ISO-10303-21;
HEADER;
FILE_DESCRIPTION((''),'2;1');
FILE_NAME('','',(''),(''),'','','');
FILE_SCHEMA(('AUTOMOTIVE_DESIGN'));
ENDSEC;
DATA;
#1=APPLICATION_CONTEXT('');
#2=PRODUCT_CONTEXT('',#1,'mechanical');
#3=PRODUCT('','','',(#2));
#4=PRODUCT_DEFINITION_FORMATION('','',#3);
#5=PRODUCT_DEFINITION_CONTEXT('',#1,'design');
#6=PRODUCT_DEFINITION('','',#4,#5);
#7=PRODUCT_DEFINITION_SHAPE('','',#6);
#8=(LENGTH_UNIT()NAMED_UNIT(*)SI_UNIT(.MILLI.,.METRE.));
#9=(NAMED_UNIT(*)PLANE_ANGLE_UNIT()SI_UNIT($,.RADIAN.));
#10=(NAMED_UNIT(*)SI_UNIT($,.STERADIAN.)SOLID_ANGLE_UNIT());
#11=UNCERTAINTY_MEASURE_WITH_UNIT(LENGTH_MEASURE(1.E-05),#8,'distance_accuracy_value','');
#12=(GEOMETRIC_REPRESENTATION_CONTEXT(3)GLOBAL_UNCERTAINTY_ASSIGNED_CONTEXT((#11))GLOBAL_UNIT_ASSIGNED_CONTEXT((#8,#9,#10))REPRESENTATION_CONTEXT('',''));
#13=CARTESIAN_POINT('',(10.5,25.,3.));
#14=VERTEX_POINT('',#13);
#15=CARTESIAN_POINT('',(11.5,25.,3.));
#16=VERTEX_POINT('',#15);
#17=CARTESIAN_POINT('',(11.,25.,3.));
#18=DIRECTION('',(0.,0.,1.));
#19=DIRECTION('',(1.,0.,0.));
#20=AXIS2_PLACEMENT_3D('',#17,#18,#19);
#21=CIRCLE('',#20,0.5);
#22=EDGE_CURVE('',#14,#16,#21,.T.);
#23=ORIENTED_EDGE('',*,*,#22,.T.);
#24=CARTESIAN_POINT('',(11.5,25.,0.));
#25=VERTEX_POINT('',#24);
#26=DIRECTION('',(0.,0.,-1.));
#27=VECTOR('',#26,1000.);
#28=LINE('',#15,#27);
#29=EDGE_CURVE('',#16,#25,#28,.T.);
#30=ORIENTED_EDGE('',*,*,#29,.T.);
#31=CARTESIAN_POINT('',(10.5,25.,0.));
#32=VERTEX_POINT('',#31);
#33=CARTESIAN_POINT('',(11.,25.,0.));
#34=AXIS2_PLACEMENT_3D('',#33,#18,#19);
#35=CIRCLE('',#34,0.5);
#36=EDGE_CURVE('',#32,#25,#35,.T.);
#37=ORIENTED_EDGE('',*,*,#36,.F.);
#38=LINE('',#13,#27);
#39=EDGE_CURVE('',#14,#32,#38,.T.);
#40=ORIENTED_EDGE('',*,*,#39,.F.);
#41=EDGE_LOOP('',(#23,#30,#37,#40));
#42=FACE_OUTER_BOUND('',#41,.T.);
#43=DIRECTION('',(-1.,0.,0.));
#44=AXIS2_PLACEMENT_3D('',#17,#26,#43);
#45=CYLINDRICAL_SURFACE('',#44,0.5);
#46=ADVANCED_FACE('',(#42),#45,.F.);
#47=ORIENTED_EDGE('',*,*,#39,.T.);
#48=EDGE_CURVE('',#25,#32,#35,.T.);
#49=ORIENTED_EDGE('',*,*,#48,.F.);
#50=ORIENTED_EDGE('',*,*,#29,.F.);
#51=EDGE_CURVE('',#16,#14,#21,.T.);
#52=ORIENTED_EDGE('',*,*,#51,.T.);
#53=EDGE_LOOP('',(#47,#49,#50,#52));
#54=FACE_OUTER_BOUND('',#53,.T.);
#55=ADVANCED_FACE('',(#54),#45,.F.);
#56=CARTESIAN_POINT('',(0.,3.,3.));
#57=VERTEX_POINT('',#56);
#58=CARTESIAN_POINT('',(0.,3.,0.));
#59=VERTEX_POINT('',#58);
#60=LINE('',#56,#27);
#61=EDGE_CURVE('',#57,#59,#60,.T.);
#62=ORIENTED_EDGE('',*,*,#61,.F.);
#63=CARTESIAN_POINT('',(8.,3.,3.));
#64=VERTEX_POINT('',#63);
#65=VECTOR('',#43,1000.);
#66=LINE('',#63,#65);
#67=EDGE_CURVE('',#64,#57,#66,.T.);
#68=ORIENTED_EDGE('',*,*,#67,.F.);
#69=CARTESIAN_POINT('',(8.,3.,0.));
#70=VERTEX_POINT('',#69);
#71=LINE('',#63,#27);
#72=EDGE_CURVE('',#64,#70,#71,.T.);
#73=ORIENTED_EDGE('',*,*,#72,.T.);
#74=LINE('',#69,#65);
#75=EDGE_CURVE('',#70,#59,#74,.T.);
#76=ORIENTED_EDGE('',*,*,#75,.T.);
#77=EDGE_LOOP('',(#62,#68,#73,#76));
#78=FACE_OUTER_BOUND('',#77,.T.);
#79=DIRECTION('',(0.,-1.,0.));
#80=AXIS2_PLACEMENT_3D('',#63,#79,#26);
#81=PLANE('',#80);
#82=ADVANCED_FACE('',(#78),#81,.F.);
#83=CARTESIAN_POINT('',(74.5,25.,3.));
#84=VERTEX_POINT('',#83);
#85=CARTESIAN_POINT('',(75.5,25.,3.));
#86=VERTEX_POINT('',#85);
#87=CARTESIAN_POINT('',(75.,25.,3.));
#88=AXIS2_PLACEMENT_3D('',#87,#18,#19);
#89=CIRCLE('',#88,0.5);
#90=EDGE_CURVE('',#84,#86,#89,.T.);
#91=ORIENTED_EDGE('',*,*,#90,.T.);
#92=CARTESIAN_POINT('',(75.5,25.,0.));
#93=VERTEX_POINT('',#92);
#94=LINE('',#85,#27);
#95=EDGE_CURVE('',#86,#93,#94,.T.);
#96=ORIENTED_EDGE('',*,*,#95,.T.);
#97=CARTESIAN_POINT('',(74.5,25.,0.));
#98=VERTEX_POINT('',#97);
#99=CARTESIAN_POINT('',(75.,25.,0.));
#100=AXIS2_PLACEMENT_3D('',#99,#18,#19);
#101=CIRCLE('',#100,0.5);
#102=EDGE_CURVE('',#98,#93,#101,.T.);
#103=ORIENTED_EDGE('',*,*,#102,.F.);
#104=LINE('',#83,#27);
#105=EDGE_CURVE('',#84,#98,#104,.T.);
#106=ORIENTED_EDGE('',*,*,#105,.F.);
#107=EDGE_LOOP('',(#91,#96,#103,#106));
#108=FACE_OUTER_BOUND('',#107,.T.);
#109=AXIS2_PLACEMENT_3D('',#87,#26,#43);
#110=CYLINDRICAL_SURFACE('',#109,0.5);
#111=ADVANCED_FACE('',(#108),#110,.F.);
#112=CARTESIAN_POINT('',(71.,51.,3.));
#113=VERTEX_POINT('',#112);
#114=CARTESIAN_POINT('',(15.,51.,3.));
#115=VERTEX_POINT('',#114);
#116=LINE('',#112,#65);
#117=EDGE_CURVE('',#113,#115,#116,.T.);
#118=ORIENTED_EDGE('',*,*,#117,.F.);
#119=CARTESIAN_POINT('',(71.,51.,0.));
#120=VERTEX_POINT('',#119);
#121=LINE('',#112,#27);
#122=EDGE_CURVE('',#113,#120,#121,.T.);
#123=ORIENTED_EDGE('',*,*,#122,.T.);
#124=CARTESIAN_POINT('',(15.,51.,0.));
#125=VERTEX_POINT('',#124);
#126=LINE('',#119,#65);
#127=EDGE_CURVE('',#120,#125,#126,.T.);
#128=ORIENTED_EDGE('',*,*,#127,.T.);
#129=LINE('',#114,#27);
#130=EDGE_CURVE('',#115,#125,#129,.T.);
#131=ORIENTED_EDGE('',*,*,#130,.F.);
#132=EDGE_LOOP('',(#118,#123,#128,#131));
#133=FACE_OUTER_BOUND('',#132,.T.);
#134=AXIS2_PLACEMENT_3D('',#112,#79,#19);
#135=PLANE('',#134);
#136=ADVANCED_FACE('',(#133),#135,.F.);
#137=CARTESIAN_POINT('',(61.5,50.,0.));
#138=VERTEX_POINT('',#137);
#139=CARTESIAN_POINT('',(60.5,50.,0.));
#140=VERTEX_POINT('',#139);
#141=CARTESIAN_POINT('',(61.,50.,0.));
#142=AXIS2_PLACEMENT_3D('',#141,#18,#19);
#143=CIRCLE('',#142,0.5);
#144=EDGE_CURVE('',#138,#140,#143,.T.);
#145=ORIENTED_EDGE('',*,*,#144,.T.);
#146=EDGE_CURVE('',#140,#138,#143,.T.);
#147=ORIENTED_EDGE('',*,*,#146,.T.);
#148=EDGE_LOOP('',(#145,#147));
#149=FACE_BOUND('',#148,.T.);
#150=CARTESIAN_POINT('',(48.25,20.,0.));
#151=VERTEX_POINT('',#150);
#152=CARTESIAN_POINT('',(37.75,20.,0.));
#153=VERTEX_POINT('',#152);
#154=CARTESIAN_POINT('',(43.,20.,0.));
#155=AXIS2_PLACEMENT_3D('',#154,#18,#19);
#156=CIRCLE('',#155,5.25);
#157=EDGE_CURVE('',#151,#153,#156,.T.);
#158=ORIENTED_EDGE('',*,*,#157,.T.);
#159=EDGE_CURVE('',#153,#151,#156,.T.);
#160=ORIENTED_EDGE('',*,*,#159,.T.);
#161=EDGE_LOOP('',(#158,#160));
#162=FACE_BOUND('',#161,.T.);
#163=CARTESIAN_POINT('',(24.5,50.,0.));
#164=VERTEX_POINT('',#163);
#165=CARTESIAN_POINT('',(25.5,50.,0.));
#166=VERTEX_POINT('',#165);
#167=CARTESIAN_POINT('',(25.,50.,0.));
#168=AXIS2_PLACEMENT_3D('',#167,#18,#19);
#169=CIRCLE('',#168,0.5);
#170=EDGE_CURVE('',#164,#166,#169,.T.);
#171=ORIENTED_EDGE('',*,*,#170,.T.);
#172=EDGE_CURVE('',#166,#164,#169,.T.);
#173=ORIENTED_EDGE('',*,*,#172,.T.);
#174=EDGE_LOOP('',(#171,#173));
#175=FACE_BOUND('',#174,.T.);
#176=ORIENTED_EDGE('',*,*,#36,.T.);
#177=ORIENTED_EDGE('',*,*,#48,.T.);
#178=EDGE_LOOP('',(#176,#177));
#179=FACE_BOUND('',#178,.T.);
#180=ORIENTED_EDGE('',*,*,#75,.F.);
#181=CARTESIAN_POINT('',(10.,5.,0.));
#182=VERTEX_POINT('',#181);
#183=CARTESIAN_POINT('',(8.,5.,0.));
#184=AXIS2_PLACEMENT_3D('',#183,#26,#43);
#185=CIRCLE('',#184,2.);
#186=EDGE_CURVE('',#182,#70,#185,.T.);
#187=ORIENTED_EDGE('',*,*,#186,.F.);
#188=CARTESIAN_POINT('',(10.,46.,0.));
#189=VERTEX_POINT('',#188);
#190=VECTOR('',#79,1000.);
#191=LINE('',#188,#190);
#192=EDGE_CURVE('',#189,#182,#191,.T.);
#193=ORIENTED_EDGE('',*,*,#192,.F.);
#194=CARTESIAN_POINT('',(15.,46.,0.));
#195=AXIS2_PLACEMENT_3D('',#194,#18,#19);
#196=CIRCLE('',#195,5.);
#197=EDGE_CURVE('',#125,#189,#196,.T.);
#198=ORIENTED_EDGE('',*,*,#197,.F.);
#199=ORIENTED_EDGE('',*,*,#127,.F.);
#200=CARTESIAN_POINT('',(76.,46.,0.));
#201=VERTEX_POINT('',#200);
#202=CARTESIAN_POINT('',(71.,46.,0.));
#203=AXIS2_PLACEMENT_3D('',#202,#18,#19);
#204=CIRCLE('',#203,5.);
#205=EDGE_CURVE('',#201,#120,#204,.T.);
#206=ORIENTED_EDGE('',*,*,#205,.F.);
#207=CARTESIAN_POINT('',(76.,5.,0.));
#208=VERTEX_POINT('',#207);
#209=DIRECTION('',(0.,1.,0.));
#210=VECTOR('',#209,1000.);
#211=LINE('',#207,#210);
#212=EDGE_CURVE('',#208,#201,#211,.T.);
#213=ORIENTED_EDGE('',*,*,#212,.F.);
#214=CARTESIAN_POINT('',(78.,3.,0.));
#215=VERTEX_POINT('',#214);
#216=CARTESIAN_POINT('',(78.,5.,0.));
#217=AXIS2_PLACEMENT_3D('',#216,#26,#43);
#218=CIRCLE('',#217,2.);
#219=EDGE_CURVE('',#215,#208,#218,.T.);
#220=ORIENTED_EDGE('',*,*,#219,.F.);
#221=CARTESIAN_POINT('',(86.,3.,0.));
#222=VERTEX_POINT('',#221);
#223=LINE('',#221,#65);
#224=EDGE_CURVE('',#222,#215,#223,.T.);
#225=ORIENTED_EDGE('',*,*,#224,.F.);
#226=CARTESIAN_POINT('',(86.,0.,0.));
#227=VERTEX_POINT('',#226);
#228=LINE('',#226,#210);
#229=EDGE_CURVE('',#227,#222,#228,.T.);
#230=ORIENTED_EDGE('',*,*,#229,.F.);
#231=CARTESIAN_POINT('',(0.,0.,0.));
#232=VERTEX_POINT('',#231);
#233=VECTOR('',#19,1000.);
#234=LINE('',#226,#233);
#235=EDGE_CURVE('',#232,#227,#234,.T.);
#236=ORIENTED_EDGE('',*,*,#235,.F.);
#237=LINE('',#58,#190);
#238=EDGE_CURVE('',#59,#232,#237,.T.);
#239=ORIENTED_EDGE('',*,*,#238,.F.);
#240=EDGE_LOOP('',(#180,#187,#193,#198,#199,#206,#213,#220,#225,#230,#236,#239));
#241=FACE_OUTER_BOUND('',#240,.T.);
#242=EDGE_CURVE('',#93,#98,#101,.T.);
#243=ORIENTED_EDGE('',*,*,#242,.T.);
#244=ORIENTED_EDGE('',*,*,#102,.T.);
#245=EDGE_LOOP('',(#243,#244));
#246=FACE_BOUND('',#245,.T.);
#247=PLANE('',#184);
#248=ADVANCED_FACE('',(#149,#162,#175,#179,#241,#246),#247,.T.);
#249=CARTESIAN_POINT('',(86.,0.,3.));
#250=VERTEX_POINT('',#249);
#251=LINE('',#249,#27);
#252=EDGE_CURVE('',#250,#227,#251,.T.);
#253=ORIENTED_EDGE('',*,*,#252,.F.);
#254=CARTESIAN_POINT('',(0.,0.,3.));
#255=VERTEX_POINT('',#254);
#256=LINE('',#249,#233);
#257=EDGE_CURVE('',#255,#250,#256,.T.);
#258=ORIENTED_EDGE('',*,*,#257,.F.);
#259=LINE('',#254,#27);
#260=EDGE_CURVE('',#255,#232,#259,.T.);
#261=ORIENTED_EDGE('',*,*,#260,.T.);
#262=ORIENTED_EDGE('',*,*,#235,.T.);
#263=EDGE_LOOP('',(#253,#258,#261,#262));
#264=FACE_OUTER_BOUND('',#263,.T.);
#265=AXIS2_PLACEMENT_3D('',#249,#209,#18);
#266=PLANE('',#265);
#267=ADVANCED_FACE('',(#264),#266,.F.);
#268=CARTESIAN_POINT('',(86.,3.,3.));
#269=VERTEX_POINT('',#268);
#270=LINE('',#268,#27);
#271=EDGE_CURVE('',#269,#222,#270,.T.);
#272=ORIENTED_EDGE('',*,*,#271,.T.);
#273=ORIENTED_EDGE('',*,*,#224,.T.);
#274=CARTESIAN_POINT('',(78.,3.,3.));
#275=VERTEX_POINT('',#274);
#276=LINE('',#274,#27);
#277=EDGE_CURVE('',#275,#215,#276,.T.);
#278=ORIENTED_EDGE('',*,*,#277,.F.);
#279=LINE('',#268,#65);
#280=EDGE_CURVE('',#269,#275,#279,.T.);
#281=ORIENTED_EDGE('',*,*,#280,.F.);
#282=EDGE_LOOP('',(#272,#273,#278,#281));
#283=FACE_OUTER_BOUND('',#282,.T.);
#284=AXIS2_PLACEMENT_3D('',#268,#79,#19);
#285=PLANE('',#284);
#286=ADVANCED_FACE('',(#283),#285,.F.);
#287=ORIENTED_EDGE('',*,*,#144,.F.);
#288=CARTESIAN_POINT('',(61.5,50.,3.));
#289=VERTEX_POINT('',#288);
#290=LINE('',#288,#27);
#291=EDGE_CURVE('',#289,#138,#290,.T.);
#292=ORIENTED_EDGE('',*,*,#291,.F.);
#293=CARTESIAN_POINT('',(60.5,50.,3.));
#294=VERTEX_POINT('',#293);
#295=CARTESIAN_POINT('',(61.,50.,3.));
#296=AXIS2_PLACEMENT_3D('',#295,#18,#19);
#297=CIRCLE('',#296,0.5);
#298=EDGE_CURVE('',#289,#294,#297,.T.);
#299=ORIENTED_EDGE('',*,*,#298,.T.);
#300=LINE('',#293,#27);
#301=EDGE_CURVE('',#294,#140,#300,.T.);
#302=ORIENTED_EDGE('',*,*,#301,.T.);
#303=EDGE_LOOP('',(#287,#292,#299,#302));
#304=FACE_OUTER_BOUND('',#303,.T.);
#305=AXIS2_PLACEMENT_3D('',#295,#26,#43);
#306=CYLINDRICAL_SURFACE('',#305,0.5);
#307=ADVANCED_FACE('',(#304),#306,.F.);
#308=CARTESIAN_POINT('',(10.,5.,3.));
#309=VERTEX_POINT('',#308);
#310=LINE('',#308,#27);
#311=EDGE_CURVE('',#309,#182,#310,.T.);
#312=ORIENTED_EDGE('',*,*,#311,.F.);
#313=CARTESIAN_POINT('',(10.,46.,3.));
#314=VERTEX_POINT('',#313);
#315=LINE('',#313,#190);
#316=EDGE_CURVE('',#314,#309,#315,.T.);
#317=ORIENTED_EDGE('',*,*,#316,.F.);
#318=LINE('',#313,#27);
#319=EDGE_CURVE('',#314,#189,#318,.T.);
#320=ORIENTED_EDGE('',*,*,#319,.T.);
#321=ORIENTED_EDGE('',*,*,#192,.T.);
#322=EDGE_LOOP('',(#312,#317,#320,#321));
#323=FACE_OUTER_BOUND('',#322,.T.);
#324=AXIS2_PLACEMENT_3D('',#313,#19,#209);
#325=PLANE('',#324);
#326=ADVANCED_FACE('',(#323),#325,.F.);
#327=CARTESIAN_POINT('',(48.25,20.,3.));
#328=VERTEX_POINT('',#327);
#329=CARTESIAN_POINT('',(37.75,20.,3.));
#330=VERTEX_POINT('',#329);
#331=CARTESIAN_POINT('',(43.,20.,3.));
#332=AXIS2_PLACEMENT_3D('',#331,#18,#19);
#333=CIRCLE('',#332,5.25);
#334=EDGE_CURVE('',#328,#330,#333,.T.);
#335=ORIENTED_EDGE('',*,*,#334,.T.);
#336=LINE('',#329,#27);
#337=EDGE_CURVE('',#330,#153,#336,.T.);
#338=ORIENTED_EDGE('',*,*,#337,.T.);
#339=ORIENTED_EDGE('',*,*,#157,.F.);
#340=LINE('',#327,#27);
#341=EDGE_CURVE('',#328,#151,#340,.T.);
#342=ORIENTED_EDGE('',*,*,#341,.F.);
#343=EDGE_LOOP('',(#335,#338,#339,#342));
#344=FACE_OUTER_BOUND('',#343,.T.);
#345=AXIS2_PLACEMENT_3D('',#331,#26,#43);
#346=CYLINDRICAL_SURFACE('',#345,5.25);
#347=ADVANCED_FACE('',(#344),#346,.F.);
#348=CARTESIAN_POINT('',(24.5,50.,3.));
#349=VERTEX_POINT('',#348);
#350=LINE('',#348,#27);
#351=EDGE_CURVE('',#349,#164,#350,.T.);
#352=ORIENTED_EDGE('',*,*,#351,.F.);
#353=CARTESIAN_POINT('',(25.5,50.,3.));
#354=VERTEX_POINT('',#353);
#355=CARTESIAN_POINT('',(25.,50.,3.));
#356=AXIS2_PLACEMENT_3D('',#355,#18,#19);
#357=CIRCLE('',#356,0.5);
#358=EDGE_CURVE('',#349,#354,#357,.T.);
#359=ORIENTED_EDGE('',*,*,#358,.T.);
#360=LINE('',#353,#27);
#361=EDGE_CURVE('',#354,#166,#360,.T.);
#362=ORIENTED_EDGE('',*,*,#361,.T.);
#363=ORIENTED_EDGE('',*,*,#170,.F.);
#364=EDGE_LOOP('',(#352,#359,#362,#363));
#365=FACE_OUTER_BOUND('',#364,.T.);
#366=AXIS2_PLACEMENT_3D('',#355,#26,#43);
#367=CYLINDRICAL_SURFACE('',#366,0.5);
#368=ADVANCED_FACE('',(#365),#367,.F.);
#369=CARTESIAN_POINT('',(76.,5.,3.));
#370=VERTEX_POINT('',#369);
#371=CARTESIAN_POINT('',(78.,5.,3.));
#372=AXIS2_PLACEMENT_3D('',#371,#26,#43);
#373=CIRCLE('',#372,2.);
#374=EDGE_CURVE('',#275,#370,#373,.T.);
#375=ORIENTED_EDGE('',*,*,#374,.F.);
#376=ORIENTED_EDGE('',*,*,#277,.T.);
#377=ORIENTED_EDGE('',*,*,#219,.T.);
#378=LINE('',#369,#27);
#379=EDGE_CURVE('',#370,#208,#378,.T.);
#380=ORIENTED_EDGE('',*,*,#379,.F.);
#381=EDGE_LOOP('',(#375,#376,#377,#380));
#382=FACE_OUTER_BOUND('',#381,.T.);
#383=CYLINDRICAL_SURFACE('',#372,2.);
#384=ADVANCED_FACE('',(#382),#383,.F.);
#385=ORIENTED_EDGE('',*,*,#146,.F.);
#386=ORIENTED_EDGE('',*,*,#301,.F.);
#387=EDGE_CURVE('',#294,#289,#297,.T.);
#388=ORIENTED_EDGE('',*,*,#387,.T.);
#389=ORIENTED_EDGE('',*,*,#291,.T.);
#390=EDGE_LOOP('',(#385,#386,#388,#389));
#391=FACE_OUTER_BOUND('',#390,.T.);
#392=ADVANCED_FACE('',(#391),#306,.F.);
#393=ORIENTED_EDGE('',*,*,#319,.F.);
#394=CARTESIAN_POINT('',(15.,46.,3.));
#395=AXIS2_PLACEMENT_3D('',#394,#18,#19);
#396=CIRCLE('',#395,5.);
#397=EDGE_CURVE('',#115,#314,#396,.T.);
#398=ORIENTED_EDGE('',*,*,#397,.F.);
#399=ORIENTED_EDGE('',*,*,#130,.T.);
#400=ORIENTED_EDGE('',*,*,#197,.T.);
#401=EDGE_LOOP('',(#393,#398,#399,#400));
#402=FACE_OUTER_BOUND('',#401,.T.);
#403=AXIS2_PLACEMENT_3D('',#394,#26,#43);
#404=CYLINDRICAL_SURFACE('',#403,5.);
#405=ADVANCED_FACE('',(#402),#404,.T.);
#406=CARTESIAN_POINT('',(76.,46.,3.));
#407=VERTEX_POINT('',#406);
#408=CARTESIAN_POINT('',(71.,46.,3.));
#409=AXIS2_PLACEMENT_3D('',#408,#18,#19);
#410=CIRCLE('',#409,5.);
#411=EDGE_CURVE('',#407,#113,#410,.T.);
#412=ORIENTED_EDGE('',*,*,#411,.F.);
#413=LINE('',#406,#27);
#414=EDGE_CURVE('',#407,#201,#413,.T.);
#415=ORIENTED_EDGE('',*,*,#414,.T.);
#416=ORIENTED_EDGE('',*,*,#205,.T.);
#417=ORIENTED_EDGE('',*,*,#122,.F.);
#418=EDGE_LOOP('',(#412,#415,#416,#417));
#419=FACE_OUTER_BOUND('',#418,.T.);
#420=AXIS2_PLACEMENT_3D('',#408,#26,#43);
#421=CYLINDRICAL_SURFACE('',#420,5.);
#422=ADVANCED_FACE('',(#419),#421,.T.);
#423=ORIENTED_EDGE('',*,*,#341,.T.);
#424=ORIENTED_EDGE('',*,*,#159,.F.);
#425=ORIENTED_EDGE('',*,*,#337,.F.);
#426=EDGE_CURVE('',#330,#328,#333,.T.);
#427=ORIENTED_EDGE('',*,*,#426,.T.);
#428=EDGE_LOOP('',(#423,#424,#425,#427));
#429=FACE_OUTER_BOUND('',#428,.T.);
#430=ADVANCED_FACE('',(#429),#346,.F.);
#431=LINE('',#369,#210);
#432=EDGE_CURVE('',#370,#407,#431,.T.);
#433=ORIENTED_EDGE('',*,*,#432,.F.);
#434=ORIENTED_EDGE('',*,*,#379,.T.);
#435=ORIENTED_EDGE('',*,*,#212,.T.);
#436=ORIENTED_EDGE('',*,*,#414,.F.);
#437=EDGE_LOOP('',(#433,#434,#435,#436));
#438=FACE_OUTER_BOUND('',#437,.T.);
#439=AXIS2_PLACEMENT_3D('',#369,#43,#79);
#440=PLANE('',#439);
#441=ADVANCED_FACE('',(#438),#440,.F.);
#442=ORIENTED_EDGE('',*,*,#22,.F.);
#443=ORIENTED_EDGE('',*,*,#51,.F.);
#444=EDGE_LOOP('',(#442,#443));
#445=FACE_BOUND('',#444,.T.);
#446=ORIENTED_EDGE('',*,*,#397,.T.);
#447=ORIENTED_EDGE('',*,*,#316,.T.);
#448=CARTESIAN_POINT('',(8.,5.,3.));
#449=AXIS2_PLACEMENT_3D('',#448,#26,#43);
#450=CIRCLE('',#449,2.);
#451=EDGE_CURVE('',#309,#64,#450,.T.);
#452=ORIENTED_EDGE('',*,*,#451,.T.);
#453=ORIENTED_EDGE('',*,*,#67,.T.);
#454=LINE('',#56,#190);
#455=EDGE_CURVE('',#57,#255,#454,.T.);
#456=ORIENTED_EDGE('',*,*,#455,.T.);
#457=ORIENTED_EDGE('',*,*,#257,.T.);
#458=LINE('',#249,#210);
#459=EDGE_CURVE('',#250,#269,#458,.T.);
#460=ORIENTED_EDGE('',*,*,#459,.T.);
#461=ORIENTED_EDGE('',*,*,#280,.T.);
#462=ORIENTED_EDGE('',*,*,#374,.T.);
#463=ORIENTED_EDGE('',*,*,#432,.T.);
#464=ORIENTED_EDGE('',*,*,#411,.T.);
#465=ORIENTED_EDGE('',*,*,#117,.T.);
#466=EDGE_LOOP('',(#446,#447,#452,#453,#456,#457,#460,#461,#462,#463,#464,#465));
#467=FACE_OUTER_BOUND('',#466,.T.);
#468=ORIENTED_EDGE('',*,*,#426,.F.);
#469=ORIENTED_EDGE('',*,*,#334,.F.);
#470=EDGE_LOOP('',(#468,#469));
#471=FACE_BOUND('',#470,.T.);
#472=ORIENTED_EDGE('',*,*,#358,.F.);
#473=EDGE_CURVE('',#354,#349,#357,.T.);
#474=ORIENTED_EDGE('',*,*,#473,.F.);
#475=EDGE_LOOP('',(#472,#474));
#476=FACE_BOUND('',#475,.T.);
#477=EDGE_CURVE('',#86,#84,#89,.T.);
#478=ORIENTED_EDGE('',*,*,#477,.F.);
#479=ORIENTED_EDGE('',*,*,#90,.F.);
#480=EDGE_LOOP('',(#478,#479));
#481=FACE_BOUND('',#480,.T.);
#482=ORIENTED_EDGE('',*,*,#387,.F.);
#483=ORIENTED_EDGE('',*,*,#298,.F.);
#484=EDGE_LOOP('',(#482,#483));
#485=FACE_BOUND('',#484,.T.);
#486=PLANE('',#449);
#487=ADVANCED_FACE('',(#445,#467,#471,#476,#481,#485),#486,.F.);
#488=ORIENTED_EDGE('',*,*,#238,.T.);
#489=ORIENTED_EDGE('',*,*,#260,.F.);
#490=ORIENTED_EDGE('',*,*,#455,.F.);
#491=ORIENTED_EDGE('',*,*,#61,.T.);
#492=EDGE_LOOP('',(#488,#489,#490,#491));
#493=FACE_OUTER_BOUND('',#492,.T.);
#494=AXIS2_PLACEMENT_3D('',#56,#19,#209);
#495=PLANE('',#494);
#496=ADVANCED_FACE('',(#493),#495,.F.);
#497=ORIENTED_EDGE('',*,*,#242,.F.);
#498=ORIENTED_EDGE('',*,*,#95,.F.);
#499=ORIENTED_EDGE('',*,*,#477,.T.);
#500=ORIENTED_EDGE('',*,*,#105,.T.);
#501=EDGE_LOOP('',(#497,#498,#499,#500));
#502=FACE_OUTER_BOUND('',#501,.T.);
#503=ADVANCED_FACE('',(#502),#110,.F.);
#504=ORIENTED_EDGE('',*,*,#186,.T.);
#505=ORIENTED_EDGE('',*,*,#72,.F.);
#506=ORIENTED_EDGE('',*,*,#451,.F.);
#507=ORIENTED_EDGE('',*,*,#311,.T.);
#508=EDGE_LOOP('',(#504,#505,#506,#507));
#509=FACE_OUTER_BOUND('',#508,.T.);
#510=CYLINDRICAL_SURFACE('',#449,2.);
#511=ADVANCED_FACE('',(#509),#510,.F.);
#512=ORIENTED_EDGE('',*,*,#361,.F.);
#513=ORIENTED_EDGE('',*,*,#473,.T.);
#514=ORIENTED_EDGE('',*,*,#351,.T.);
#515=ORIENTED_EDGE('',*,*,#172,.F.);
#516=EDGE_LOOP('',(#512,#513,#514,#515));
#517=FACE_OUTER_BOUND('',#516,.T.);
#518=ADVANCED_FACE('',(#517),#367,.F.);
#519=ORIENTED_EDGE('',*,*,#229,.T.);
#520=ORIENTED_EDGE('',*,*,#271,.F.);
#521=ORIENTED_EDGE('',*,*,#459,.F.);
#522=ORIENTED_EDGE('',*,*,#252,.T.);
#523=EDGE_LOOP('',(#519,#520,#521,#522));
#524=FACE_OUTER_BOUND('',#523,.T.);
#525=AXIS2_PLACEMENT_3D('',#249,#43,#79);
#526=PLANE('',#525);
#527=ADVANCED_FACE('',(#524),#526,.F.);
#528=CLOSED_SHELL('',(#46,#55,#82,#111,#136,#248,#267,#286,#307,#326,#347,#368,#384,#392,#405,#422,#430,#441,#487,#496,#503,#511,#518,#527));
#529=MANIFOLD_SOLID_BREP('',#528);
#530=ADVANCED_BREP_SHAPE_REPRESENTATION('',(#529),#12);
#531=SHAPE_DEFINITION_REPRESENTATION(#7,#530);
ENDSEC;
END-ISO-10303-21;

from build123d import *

# Parameters (mm, degrees)
SKETCH1_R           = 5.25
SKETCH1_R_2         = 0.5
BOSS_EXTRUDE1_DEPTH = 3


with BuildPart() as part:
    # Sketch1 → Boss-Extrude1 (new body)
    with BuildSketch(Plane.XY):
        with BuildLine():
            Line((86, 0), (86, 3))
            Line((86, 3), (78, 3))
            ThreePointArc((78, 3), (76.585786438, 3.585786438), (76, 5))
            Line((76, 5), (76, 46))
            ThreePointArc((76, 46), (74.535533906, 49.535533906), (71, 51))
            Line((71, 51), (15, 51))
            ThreePointArc((15, 51), (11.464466094, 49.535533906), (10, 46))
            Line((10, 46), (10, 5))
            ThreePointArc((10, 5), (9.414213562, 3.585786438), (8, 3))
            Line((8, 3), (0, 3))
            Line((0, 3), (0, 0))
            Line((0, 0), (86, 0))
        make_face()
        with Locations((43, 20)):
            Circle(SKETCH1_R, mode=Mode.SUBTRACT)
        with Locations((25, 50)):
            Circle(SKETCH1_R_2, mode=Mode.SUBTRACT)
        with Locations((61, 50)):
            Circle(SKETCH1_R_2, mode=Mode.SUBTRACT)
        with Locations((75, 25)):
            Circle(SKETCH1_R_2, mode=Mode.SUBTRACT)
        with Locations((11, 25)):
            Circle(SKETCH1_R_2, mode=Mode.SUBTRACT)
    extrude(amount=BOSS_EXTRUDE1_DEPTH)


solid = part.part
